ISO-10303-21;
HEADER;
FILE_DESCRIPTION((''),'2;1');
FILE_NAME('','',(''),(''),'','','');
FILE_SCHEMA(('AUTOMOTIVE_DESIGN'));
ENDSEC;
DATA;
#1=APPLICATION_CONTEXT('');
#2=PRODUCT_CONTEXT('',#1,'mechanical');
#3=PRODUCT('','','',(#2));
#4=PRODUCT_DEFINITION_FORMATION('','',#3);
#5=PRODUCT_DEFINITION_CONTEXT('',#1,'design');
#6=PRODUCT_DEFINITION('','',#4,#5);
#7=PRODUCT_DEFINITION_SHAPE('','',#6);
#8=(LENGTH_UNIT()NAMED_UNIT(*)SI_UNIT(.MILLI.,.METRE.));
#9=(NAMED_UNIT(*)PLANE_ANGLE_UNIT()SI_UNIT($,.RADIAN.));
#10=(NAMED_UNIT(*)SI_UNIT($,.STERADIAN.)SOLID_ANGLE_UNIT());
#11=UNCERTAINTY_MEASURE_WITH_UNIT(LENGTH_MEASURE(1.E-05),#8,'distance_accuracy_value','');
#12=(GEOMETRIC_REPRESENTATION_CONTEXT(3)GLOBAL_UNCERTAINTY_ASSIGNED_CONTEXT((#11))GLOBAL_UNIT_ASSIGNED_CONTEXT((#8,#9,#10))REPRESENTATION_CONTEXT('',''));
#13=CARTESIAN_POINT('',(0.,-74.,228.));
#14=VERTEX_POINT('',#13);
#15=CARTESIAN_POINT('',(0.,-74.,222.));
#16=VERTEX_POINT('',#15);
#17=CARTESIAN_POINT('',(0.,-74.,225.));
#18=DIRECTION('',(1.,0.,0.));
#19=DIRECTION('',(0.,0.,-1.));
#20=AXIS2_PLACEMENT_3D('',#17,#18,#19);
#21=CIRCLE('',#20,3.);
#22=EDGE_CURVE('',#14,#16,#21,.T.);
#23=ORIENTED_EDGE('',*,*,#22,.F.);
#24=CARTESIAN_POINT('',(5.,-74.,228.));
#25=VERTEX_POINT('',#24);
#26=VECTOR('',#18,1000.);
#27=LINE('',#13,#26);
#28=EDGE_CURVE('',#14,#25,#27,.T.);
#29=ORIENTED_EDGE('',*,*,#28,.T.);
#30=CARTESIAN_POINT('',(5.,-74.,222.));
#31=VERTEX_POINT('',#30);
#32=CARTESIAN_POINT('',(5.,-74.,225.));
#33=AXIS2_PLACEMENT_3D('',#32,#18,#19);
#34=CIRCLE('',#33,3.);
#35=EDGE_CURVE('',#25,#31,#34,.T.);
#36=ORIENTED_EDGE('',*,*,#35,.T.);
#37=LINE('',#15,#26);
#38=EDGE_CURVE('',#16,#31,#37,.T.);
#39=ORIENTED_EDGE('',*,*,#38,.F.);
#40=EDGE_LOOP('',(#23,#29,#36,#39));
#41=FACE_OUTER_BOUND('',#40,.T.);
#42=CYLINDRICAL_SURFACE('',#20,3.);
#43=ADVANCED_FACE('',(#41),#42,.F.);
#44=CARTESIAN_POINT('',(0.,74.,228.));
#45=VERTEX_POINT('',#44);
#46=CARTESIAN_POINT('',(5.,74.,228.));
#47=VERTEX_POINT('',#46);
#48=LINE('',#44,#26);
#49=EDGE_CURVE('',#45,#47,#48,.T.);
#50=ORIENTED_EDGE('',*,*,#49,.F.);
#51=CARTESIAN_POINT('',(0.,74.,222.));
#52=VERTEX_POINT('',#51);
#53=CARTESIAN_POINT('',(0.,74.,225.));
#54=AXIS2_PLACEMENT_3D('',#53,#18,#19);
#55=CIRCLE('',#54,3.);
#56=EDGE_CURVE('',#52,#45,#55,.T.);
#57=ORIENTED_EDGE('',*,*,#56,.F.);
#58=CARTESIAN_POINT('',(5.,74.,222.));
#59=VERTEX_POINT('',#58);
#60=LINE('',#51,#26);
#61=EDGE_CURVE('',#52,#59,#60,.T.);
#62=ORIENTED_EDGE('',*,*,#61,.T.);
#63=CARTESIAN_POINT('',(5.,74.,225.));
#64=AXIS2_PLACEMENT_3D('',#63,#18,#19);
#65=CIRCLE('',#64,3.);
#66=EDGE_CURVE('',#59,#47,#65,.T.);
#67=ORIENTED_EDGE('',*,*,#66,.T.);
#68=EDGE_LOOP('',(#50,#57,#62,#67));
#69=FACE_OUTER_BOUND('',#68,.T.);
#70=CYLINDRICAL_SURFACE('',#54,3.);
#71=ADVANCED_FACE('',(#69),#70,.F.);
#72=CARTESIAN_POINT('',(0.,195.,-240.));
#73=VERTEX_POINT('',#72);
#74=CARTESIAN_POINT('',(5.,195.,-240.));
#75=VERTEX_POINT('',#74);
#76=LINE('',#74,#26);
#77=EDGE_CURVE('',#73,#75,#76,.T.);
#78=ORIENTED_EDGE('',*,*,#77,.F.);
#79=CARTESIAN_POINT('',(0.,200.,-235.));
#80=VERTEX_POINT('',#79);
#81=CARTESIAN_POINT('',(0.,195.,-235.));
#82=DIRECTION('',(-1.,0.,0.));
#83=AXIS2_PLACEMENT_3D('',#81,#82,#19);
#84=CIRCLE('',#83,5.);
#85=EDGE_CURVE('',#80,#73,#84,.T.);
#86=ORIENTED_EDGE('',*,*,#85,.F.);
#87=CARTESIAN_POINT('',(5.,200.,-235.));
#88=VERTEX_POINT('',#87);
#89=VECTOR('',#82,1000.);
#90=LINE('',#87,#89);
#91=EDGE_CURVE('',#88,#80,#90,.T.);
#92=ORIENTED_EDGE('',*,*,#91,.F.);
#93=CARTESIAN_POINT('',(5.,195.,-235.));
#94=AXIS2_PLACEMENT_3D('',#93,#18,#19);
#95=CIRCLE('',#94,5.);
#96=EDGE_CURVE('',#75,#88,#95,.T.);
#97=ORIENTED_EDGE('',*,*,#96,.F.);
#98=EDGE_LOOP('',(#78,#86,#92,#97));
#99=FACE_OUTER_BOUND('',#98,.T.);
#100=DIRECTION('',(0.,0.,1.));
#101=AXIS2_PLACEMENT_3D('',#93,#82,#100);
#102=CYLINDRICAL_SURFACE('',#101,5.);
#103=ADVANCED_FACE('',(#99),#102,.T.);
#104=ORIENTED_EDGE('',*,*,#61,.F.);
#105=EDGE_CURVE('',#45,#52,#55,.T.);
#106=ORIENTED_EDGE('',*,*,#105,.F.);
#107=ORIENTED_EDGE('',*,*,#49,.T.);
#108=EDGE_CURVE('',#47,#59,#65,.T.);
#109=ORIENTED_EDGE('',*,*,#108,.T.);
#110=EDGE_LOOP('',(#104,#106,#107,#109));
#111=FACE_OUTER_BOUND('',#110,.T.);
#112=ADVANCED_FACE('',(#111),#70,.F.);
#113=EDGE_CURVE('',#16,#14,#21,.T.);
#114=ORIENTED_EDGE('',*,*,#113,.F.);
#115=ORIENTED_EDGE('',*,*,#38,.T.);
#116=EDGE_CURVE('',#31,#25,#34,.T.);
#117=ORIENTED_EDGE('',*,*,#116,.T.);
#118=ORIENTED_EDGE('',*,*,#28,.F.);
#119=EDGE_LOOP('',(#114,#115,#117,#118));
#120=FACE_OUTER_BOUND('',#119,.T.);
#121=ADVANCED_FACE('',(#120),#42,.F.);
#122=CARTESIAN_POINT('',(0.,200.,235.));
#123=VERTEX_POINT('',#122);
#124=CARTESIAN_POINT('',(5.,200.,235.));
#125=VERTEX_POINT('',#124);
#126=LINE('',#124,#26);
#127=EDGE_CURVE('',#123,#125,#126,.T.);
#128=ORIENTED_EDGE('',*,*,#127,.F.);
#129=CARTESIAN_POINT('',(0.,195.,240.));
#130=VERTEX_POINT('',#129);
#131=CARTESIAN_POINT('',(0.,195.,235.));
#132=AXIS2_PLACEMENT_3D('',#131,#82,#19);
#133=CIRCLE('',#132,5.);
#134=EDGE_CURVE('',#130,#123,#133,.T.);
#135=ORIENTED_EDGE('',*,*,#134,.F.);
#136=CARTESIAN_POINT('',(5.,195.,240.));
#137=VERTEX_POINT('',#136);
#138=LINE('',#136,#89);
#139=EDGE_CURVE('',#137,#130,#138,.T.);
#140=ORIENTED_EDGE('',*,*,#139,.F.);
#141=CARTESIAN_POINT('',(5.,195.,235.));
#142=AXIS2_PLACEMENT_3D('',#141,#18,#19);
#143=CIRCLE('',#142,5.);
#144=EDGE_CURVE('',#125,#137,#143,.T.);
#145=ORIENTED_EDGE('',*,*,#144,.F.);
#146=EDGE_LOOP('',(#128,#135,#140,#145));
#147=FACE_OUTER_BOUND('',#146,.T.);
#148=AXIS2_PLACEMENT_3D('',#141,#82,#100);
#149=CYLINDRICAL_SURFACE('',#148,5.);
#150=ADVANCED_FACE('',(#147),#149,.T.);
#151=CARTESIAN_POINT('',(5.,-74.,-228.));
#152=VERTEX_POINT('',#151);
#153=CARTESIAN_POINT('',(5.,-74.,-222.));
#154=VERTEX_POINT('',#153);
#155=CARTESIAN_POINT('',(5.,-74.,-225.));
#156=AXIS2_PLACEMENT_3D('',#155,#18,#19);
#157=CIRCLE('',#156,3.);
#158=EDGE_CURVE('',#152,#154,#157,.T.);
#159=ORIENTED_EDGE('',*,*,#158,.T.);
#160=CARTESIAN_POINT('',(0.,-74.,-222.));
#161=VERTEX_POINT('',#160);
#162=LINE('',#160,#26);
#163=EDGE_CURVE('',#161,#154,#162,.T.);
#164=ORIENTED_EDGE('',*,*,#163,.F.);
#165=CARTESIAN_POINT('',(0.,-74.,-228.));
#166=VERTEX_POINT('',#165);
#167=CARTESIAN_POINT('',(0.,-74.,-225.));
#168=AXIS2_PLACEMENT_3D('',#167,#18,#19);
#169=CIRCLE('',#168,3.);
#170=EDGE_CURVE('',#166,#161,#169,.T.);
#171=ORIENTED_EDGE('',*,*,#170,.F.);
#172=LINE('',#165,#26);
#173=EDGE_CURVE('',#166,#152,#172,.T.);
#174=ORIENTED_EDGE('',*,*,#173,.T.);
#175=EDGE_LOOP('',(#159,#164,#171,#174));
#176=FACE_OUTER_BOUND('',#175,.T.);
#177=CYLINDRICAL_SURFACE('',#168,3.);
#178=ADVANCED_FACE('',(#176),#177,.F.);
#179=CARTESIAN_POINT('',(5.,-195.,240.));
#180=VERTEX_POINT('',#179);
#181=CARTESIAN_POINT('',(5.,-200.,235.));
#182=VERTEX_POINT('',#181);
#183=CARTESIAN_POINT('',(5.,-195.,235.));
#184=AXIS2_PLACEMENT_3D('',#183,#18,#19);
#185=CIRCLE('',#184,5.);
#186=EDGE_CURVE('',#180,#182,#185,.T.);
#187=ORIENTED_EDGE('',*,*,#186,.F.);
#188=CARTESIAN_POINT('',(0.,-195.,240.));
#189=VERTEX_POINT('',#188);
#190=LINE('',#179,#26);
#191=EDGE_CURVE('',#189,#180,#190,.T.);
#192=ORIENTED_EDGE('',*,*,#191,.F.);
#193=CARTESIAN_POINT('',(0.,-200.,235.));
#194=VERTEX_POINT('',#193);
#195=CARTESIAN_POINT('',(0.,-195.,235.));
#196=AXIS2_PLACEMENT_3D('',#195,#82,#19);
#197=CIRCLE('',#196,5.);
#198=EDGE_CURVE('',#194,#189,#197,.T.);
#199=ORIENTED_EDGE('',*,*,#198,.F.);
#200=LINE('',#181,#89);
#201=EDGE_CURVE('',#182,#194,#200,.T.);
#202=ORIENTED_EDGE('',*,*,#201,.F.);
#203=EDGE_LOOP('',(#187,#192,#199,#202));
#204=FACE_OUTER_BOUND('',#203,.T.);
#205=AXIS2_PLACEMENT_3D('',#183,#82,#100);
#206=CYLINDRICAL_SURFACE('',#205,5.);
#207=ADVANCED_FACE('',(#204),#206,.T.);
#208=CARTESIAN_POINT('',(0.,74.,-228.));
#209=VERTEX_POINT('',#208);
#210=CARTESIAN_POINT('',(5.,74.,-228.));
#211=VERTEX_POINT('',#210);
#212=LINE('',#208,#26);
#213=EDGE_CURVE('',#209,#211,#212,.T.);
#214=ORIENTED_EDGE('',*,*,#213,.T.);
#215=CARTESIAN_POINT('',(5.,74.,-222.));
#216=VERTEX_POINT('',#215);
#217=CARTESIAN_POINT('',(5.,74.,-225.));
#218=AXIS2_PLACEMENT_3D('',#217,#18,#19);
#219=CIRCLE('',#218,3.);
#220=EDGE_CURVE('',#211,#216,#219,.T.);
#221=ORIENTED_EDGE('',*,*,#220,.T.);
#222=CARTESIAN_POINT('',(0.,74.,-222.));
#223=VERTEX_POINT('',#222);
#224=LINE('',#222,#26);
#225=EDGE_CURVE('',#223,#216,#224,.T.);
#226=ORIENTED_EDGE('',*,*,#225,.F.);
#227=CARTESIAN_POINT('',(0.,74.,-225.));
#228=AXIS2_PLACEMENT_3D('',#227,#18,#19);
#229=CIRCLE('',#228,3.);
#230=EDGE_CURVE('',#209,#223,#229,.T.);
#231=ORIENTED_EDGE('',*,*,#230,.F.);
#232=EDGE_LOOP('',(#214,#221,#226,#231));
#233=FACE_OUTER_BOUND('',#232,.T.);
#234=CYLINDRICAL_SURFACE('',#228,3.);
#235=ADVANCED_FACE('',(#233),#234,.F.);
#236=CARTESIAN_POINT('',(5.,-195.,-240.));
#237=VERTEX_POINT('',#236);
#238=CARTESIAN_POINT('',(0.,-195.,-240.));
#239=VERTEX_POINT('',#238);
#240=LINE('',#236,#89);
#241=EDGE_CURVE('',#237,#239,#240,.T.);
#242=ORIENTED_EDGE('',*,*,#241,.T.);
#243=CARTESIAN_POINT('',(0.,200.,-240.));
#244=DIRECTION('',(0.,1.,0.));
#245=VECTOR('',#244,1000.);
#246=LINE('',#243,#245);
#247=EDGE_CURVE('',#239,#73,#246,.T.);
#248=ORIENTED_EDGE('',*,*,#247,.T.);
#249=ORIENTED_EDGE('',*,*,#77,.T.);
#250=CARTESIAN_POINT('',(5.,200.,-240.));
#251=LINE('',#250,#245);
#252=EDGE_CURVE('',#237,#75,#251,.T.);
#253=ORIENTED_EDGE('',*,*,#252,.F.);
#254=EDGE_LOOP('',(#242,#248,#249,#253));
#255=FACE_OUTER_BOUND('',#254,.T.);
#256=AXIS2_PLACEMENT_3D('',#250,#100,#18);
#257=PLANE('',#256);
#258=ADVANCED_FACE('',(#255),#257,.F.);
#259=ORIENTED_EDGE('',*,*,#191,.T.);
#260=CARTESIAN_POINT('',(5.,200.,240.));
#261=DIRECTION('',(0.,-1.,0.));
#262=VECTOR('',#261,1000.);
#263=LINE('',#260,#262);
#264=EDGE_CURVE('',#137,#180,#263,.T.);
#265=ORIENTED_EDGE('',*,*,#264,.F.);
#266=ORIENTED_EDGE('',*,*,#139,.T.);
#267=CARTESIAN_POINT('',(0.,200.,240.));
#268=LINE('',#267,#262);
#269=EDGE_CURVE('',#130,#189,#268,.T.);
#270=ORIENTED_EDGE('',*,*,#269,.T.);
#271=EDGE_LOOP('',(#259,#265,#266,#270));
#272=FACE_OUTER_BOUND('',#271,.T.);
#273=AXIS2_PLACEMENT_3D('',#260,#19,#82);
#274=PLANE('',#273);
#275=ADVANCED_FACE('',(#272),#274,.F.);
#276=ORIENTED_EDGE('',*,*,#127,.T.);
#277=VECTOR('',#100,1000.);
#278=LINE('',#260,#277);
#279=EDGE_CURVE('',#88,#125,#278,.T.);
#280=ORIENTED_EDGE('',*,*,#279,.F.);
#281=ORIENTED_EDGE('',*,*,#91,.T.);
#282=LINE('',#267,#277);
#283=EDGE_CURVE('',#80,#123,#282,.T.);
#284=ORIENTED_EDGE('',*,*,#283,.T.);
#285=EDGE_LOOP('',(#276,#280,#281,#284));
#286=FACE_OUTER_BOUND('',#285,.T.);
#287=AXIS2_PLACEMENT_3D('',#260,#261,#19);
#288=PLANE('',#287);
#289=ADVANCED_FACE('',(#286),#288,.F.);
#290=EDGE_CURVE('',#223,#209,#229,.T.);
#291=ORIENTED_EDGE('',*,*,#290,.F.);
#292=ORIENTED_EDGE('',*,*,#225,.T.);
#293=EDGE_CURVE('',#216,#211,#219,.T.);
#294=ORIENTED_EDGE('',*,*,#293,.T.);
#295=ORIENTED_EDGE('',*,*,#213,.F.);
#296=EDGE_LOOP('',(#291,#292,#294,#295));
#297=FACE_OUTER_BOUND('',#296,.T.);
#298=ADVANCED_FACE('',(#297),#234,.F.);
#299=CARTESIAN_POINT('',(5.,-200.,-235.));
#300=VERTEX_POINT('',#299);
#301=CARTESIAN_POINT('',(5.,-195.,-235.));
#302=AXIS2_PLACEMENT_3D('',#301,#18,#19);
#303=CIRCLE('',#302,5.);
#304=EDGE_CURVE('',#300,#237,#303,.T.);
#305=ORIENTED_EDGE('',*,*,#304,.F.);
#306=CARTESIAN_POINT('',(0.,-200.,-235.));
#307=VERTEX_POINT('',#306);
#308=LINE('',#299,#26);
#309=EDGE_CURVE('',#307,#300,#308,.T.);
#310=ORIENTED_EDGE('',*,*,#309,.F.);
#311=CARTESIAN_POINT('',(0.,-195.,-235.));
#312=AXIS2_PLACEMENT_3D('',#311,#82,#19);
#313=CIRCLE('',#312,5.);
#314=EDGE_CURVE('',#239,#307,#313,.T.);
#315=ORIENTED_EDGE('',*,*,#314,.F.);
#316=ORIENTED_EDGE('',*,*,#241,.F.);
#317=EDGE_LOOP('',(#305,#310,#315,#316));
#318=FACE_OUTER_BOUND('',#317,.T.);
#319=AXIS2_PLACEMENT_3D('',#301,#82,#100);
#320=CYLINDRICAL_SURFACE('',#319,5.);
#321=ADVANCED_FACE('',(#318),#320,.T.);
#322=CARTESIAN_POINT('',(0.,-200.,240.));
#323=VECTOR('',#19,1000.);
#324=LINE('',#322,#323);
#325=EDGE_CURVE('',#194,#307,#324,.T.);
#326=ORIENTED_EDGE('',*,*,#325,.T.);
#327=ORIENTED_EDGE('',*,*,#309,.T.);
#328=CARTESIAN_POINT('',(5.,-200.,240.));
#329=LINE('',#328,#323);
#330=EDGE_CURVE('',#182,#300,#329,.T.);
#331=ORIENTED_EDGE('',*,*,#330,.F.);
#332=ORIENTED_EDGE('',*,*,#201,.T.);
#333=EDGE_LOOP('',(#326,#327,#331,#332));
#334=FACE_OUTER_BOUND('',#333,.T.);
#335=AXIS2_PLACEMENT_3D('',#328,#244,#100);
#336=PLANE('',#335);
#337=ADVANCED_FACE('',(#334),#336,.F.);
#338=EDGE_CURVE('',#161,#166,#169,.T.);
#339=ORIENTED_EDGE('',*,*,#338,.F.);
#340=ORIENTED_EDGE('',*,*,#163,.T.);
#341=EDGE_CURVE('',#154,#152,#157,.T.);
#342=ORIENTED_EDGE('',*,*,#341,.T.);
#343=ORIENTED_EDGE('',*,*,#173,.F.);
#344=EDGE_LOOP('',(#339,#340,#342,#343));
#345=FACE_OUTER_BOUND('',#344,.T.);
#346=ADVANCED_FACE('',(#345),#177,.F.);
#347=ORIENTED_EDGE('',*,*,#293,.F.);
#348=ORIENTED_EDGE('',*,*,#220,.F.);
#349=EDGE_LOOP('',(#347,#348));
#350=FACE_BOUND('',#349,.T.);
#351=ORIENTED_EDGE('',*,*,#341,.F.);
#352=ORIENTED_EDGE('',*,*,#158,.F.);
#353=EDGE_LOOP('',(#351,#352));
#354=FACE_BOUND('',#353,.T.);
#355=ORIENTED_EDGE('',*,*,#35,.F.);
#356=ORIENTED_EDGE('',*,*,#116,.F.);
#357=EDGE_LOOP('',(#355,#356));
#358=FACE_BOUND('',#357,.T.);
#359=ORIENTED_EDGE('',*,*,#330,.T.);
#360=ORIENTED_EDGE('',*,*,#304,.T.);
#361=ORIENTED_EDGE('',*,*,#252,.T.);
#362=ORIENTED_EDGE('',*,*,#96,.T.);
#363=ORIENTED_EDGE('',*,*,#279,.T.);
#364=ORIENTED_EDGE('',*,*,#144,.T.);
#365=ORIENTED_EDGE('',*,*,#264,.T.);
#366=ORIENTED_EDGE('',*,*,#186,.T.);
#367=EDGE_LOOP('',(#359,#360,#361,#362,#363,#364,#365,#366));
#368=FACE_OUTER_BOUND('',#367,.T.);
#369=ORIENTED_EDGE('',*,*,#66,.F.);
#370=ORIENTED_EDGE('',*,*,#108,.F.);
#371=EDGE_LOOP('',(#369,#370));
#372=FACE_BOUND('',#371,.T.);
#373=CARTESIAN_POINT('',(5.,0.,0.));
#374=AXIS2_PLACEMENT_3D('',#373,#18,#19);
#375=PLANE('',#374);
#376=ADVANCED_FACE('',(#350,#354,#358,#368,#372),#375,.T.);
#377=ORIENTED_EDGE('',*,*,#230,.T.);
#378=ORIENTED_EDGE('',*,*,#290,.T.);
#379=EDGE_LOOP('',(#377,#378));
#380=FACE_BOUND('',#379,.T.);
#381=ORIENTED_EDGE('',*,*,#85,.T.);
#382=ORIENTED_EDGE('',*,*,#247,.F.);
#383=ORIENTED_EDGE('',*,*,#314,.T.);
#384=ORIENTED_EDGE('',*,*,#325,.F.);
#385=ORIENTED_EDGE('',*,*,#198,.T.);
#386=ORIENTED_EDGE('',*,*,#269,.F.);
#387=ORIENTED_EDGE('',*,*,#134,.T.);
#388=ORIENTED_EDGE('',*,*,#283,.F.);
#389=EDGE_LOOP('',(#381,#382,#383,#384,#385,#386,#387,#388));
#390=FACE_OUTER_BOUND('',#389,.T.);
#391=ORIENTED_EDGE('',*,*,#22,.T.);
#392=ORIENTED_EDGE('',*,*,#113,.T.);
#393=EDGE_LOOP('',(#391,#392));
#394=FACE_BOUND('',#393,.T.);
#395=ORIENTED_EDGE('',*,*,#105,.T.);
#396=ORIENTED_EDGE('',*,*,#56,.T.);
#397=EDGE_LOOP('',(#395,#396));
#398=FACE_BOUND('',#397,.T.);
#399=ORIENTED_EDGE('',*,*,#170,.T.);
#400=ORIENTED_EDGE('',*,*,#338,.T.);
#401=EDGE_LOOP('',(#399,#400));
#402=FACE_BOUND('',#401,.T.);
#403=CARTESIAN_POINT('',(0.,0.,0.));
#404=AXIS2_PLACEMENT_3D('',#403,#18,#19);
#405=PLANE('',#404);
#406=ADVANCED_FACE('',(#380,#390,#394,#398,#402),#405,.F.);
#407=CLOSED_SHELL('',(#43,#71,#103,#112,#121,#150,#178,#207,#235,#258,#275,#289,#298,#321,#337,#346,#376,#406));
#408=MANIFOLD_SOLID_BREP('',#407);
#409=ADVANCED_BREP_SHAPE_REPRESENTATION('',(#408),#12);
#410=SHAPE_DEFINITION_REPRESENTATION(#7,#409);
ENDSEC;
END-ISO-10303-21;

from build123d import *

# Parameters (mm, degrees)
SKETCH_1_W          = 480
SKETCH_1_H          = 400
EXTRUDE_1_DEPTH     = 5
SKETCH_2_R          = 3
CUT_EXTRUDE_1_DEPTH = 313.449995999
FILLET_1_R          = 5


with BuildPart() as part:
    # 草图1 → 凸台-拉伸1 (new body)
    with BuildSketch(Plane(origin=(0, 0, 0), x_dir=(0, 0, -1), z_dir=(1, 0, 0))):
        Rectangle(SKETCH_1_W, SKETCH_1_H)
    extrude(amount=EXTRUDE_1_DEPTH)

    # 草图2 → 切除-拉伸1 (cut, through all)
    with BuildSketch(Plane(origin=(5, 0, 0), x_dir=(0, 0, -1), z_dir=(1, 0, 0))):
        with Locations((-225, 74)):
            Circle(SKETCH_2_R)
        with Locations((225, 74)):
            Circle(SKETCH_2_R)
        with Locations((-225, -74)):
            Circle(SKETCH_2_R)
        with Locations((225, -74)):
            Circle(SKETCH_2_R)
    extrude(amount=-CUT_EXTRUDE_1_DEPTH, mode=Mode.SUBTRACT)

    # 圆角1
    fillet_1_edges = [part.edges().sort_by_distance(p)[0] for p in [
        (2.5, 200, 240),
        (2.5, 200, -240),
        (2.5, -200, -240),
        (2.5, -200, 240),
    ]]
    fillet(fillet_1_edges, radius=FILLET_1_R)


solid = part.part
